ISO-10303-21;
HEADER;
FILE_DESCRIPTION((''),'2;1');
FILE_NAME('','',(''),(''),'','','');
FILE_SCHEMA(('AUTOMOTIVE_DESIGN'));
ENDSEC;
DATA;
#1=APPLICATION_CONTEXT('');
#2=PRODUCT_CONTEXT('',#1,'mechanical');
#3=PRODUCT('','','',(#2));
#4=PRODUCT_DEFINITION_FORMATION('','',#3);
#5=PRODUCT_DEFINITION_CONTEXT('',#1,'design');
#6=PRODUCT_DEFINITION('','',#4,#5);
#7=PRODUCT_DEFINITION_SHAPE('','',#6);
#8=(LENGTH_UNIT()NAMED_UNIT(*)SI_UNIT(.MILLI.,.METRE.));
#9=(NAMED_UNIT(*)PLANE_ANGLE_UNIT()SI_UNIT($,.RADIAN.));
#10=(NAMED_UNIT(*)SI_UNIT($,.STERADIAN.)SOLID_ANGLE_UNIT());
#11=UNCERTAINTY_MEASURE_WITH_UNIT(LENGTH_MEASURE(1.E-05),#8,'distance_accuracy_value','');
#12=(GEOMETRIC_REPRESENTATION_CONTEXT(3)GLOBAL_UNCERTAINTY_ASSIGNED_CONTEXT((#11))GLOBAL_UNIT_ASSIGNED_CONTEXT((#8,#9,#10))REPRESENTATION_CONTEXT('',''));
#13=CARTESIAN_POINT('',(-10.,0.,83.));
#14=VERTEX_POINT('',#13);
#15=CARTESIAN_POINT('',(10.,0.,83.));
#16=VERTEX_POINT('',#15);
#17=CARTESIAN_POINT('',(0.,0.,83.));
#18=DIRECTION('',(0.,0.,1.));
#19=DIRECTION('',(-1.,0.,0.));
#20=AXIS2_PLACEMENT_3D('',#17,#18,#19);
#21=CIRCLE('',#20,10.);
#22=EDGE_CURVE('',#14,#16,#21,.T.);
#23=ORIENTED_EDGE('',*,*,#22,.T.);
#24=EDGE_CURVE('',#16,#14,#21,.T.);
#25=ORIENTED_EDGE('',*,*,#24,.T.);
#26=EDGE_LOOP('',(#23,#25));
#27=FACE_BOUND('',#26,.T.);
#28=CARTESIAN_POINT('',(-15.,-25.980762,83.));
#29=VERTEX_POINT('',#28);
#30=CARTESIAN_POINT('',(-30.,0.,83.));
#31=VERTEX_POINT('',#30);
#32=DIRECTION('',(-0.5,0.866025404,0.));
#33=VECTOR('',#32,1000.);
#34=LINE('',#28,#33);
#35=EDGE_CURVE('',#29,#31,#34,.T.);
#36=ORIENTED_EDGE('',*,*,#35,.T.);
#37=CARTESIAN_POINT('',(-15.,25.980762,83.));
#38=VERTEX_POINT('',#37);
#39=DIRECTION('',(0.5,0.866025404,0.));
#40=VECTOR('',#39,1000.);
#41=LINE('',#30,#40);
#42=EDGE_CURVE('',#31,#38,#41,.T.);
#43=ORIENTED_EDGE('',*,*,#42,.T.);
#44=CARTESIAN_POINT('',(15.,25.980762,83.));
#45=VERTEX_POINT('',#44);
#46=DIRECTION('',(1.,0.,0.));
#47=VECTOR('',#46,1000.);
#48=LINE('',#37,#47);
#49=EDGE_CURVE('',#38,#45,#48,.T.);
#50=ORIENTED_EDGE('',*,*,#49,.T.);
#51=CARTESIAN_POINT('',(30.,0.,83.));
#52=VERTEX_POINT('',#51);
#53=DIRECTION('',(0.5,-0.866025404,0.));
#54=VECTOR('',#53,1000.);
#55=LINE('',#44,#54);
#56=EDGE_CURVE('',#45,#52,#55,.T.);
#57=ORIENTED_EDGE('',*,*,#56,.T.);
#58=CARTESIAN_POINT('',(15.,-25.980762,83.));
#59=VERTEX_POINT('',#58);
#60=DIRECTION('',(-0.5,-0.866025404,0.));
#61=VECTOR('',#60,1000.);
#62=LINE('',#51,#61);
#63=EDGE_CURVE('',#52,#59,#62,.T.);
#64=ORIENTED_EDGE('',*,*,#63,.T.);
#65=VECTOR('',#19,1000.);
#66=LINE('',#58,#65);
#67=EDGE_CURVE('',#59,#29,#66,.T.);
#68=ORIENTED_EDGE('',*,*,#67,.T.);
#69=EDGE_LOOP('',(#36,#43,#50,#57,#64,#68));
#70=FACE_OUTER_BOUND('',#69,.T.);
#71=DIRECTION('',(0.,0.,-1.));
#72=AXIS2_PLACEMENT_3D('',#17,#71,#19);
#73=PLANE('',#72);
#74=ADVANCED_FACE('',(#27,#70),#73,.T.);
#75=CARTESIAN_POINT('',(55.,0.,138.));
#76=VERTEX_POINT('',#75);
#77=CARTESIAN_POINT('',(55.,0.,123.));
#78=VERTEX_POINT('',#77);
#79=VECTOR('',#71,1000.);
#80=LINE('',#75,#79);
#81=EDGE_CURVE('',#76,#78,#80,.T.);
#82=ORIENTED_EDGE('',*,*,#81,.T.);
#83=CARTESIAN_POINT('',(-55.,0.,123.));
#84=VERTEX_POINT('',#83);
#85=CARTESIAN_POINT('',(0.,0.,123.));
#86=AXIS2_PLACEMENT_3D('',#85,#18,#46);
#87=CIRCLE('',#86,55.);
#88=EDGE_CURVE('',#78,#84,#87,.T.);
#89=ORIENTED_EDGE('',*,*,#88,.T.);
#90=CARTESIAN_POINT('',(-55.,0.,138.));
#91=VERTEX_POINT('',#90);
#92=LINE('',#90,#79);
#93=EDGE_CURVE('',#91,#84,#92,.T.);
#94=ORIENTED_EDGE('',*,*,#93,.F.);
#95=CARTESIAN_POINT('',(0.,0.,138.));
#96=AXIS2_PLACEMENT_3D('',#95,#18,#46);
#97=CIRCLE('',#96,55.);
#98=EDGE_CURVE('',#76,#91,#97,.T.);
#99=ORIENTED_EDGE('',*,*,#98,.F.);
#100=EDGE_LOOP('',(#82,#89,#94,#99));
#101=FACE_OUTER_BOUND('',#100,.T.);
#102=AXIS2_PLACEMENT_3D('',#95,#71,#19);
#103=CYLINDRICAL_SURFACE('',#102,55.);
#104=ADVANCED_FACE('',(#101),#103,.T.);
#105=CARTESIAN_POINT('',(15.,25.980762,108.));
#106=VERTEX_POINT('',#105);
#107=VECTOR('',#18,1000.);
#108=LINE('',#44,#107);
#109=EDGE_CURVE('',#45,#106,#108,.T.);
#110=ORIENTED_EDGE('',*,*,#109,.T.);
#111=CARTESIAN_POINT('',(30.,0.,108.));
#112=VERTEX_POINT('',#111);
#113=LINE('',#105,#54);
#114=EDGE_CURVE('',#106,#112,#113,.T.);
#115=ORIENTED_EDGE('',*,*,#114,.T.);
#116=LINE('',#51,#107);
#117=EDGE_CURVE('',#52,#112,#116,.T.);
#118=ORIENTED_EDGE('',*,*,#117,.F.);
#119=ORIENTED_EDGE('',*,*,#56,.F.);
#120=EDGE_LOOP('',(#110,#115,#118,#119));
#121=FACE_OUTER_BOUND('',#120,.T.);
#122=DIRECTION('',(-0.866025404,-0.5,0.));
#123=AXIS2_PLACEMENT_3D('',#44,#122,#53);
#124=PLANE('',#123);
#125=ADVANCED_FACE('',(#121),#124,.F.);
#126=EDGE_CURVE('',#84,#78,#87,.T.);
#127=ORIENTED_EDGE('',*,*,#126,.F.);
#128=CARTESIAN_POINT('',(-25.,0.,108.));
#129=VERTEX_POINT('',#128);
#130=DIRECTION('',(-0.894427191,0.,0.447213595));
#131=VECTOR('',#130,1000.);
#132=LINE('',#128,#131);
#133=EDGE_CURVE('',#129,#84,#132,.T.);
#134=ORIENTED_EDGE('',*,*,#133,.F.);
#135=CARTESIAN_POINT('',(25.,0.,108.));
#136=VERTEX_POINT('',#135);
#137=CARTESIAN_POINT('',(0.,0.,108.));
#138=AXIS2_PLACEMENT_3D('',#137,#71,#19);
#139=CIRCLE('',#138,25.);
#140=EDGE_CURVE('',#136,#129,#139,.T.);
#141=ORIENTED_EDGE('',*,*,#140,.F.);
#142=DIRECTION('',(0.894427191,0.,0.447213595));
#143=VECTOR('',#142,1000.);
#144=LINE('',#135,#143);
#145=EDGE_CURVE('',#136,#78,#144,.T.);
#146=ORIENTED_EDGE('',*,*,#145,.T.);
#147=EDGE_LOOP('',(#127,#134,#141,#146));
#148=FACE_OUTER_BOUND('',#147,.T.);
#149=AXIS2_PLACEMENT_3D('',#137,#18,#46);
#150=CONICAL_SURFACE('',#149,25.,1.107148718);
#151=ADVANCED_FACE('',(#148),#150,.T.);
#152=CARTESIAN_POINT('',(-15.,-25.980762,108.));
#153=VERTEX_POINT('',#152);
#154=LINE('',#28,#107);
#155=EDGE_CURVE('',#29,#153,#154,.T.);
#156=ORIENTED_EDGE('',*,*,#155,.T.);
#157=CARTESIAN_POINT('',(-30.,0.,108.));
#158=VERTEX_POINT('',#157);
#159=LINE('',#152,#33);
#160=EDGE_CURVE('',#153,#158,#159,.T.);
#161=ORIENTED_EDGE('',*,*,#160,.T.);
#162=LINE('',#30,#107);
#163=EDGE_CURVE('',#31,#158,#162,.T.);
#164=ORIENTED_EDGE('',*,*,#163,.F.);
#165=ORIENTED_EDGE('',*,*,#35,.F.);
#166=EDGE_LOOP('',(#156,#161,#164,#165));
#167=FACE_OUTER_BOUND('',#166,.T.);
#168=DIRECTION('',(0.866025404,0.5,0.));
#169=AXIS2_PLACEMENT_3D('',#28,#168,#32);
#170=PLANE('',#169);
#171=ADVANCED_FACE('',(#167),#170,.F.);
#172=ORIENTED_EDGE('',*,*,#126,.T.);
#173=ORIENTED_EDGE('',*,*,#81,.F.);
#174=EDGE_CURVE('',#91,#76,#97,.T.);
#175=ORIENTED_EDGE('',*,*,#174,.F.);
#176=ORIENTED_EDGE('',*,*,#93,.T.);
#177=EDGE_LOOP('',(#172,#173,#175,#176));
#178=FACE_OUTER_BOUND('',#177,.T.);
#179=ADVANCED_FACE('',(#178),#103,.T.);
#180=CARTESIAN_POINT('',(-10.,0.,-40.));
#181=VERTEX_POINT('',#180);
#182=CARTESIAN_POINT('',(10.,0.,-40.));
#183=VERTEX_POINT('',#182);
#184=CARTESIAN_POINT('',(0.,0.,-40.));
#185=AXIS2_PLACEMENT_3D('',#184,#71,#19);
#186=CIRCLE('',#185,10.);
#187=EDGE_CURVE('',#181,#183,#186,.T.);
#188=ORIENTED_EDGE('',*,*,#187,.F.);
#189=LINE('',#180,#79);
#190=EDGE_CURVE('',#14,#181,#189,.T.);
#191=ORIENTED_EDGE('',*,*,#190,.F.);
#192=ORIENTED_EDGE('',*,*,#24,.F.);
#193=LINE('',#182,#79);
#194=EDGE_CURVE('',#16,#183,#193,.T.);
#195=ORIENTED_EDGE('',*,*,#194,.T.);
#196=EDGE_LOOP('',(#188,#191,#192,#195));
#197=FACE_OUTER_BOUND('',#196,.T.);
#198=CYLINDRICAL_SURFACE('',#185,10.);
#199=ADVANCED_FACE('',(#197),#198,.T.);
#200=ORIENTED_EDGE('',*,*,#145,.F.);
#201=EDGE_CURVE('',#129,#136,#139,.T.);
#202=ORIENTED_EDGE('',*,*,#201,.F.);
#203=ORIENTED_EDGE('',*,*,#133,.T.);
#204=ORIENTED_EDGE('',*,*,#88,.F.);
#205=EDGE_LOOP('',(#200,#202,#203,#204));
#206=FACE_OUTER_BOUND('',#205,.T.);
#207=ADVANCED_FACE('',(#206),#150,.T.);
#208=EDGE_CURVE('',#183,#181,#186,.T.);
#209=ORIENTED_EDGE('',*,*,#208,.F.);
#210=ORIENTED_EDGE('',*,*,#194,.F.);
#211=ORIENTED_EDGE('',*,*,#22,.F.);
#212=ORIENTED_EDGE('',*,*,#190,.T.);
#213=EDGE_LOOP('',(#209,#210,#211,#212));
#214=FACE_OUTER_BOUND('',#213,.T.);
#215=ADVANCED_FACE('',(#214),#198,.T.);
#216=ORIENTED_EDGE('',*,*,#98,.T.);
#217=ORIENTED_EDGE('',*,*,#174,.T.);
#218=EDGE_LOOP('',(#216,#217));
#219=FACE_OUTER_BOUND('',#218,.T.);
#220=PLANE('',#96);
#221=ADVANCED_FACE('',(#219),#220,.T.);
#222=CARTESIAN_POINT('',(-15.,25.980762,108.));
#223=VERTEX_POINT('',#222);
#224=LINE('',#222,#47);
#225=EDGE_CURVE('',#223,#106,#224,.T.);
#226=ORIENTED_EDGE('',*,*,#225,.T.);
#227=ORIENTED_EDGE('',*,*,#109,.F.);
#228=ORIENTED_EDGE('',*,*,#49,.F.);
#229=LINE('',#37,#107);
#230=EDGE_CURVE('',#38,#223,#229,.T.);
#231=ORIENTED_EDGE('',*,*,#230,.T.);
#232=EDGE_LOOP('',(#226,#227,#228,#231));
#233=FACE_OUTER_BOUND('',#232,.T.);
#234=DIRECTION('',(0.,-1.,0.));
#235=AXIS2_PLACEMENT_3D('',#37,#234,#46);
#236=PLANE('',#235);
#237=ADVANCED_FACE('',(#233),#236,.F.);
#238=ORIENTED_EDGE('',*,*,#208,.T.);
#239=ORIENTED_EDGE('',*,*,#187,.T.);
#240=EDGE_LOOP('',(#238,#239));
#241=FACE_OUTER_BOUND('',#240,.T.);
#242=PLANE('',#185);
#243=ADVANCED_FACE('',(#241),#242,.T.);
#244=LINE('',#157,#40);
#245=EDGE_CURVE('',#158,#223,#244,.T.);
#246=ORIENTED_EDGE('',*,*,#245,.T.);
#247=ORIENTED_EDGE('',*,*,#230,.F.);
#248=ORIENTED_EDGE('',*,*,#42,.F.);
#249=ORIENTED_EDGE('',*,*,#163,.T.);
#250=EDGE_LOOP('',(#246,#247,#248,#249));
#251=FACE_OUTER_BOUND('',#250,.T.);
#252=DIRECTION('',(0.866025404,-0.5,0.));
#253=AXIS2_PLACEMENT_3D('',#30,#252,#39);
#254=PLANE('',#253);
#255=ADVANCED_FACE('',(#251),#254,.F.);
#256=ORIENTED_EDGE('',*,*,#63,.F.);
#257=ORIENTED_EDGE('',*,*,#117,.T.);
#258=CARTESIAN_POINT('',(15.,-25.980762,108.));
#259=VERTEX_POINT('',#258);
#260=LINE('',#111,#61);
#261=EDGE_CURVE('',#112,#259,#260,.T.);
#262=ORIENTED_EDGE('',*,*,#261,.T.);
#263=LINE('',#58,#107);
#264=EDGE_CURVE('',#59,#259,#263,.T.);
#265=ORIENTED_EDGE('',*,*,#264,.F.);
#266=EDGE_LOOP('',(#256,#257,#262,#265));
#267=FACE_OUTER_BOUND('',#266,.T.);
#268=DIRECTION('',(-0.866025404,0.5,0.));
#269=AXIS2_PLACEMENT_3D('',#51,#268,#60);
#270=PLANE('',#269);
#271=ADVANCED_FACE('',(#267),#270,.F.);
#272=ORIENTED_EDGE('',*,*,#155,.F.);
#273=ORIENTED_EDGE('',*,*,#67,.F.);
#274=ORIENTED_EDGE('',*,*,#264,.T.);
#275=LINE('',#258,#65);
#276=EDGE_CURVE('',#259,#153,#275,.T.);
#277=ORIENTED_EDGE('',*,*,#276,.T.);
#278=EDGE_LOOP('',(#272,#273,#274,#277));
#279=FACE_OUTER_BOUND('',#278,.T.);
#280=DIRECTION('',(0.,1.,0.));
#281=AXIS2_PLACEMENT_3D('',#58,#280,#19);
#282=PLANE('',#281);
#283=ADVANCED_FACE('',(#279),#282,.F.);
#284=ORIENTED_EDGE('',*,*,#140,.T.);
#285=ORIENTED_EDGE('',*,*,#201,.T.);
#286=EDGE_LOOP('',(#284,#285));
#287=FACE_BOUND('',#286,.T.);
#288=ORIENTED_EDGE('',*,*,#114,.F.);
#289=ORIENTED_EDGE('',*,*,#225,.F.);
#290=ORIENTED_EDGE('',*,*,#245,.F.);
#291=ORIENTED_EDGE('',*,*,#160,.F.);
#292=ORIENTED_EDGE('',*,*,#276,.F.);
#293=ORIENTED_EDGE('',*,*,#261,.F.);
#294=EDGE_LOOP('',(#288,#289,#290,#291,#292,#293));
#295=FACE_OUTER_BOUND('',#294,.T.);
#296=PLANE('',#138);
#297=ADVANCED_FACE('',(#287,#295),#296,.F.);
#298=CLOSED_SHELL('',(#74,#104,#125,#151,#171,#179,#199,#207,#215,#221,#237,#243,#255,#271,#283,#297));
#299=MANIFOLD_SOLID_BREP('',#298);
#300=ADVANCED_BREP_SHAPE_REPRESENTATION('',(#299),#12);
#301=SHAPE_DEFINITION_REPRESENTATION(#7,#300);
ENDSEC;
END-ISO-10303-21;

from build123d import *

# Parameters (mm, degrees)
SKETCH_2_R      = 55
EXTRUDE_1_DEPTH = 15
EXTRUDE_2_DEPTH = 25


with BuildPart() as part:
    # 草图1 → 旋转1 (revolve)
    with BuildSketch(Plane(origin=(0, 0, 0), x_dir=(1, 0, 0), z_dir=(0, 1, 0))):
        Polygon((0, 40), (-10, 40), (-10, -108), (-25, -108), (-55, -123), (0, -123), align=None)
    revolve(axis=Axis((0, 0, -40), (0, 0, 1)))

    # 草图2 → 凸台-拉伸1 (add)
    with BuildSketch(Plane.XY.offset(123)):
        Circle(SKETCH_2_R)
    extrude(amount=EXTRUDE_1_DEPTH)

    # 草图3 → 凸台-拉伸2 (add)
    with BuildSketch(Plane(origin=(0, 0, 108), x_dir=(-1, 0, 0), z_dir=(0, 0, -1))):
        Polygon((15, 25.980762114), (-15, 25.980762114), (-30, 0), (-15, -25.980762114), (15, -25.980762114), (30, 0), align=None)
    extrude(amount=EXTRUDE_2_DEPTH)


solid = part.part
